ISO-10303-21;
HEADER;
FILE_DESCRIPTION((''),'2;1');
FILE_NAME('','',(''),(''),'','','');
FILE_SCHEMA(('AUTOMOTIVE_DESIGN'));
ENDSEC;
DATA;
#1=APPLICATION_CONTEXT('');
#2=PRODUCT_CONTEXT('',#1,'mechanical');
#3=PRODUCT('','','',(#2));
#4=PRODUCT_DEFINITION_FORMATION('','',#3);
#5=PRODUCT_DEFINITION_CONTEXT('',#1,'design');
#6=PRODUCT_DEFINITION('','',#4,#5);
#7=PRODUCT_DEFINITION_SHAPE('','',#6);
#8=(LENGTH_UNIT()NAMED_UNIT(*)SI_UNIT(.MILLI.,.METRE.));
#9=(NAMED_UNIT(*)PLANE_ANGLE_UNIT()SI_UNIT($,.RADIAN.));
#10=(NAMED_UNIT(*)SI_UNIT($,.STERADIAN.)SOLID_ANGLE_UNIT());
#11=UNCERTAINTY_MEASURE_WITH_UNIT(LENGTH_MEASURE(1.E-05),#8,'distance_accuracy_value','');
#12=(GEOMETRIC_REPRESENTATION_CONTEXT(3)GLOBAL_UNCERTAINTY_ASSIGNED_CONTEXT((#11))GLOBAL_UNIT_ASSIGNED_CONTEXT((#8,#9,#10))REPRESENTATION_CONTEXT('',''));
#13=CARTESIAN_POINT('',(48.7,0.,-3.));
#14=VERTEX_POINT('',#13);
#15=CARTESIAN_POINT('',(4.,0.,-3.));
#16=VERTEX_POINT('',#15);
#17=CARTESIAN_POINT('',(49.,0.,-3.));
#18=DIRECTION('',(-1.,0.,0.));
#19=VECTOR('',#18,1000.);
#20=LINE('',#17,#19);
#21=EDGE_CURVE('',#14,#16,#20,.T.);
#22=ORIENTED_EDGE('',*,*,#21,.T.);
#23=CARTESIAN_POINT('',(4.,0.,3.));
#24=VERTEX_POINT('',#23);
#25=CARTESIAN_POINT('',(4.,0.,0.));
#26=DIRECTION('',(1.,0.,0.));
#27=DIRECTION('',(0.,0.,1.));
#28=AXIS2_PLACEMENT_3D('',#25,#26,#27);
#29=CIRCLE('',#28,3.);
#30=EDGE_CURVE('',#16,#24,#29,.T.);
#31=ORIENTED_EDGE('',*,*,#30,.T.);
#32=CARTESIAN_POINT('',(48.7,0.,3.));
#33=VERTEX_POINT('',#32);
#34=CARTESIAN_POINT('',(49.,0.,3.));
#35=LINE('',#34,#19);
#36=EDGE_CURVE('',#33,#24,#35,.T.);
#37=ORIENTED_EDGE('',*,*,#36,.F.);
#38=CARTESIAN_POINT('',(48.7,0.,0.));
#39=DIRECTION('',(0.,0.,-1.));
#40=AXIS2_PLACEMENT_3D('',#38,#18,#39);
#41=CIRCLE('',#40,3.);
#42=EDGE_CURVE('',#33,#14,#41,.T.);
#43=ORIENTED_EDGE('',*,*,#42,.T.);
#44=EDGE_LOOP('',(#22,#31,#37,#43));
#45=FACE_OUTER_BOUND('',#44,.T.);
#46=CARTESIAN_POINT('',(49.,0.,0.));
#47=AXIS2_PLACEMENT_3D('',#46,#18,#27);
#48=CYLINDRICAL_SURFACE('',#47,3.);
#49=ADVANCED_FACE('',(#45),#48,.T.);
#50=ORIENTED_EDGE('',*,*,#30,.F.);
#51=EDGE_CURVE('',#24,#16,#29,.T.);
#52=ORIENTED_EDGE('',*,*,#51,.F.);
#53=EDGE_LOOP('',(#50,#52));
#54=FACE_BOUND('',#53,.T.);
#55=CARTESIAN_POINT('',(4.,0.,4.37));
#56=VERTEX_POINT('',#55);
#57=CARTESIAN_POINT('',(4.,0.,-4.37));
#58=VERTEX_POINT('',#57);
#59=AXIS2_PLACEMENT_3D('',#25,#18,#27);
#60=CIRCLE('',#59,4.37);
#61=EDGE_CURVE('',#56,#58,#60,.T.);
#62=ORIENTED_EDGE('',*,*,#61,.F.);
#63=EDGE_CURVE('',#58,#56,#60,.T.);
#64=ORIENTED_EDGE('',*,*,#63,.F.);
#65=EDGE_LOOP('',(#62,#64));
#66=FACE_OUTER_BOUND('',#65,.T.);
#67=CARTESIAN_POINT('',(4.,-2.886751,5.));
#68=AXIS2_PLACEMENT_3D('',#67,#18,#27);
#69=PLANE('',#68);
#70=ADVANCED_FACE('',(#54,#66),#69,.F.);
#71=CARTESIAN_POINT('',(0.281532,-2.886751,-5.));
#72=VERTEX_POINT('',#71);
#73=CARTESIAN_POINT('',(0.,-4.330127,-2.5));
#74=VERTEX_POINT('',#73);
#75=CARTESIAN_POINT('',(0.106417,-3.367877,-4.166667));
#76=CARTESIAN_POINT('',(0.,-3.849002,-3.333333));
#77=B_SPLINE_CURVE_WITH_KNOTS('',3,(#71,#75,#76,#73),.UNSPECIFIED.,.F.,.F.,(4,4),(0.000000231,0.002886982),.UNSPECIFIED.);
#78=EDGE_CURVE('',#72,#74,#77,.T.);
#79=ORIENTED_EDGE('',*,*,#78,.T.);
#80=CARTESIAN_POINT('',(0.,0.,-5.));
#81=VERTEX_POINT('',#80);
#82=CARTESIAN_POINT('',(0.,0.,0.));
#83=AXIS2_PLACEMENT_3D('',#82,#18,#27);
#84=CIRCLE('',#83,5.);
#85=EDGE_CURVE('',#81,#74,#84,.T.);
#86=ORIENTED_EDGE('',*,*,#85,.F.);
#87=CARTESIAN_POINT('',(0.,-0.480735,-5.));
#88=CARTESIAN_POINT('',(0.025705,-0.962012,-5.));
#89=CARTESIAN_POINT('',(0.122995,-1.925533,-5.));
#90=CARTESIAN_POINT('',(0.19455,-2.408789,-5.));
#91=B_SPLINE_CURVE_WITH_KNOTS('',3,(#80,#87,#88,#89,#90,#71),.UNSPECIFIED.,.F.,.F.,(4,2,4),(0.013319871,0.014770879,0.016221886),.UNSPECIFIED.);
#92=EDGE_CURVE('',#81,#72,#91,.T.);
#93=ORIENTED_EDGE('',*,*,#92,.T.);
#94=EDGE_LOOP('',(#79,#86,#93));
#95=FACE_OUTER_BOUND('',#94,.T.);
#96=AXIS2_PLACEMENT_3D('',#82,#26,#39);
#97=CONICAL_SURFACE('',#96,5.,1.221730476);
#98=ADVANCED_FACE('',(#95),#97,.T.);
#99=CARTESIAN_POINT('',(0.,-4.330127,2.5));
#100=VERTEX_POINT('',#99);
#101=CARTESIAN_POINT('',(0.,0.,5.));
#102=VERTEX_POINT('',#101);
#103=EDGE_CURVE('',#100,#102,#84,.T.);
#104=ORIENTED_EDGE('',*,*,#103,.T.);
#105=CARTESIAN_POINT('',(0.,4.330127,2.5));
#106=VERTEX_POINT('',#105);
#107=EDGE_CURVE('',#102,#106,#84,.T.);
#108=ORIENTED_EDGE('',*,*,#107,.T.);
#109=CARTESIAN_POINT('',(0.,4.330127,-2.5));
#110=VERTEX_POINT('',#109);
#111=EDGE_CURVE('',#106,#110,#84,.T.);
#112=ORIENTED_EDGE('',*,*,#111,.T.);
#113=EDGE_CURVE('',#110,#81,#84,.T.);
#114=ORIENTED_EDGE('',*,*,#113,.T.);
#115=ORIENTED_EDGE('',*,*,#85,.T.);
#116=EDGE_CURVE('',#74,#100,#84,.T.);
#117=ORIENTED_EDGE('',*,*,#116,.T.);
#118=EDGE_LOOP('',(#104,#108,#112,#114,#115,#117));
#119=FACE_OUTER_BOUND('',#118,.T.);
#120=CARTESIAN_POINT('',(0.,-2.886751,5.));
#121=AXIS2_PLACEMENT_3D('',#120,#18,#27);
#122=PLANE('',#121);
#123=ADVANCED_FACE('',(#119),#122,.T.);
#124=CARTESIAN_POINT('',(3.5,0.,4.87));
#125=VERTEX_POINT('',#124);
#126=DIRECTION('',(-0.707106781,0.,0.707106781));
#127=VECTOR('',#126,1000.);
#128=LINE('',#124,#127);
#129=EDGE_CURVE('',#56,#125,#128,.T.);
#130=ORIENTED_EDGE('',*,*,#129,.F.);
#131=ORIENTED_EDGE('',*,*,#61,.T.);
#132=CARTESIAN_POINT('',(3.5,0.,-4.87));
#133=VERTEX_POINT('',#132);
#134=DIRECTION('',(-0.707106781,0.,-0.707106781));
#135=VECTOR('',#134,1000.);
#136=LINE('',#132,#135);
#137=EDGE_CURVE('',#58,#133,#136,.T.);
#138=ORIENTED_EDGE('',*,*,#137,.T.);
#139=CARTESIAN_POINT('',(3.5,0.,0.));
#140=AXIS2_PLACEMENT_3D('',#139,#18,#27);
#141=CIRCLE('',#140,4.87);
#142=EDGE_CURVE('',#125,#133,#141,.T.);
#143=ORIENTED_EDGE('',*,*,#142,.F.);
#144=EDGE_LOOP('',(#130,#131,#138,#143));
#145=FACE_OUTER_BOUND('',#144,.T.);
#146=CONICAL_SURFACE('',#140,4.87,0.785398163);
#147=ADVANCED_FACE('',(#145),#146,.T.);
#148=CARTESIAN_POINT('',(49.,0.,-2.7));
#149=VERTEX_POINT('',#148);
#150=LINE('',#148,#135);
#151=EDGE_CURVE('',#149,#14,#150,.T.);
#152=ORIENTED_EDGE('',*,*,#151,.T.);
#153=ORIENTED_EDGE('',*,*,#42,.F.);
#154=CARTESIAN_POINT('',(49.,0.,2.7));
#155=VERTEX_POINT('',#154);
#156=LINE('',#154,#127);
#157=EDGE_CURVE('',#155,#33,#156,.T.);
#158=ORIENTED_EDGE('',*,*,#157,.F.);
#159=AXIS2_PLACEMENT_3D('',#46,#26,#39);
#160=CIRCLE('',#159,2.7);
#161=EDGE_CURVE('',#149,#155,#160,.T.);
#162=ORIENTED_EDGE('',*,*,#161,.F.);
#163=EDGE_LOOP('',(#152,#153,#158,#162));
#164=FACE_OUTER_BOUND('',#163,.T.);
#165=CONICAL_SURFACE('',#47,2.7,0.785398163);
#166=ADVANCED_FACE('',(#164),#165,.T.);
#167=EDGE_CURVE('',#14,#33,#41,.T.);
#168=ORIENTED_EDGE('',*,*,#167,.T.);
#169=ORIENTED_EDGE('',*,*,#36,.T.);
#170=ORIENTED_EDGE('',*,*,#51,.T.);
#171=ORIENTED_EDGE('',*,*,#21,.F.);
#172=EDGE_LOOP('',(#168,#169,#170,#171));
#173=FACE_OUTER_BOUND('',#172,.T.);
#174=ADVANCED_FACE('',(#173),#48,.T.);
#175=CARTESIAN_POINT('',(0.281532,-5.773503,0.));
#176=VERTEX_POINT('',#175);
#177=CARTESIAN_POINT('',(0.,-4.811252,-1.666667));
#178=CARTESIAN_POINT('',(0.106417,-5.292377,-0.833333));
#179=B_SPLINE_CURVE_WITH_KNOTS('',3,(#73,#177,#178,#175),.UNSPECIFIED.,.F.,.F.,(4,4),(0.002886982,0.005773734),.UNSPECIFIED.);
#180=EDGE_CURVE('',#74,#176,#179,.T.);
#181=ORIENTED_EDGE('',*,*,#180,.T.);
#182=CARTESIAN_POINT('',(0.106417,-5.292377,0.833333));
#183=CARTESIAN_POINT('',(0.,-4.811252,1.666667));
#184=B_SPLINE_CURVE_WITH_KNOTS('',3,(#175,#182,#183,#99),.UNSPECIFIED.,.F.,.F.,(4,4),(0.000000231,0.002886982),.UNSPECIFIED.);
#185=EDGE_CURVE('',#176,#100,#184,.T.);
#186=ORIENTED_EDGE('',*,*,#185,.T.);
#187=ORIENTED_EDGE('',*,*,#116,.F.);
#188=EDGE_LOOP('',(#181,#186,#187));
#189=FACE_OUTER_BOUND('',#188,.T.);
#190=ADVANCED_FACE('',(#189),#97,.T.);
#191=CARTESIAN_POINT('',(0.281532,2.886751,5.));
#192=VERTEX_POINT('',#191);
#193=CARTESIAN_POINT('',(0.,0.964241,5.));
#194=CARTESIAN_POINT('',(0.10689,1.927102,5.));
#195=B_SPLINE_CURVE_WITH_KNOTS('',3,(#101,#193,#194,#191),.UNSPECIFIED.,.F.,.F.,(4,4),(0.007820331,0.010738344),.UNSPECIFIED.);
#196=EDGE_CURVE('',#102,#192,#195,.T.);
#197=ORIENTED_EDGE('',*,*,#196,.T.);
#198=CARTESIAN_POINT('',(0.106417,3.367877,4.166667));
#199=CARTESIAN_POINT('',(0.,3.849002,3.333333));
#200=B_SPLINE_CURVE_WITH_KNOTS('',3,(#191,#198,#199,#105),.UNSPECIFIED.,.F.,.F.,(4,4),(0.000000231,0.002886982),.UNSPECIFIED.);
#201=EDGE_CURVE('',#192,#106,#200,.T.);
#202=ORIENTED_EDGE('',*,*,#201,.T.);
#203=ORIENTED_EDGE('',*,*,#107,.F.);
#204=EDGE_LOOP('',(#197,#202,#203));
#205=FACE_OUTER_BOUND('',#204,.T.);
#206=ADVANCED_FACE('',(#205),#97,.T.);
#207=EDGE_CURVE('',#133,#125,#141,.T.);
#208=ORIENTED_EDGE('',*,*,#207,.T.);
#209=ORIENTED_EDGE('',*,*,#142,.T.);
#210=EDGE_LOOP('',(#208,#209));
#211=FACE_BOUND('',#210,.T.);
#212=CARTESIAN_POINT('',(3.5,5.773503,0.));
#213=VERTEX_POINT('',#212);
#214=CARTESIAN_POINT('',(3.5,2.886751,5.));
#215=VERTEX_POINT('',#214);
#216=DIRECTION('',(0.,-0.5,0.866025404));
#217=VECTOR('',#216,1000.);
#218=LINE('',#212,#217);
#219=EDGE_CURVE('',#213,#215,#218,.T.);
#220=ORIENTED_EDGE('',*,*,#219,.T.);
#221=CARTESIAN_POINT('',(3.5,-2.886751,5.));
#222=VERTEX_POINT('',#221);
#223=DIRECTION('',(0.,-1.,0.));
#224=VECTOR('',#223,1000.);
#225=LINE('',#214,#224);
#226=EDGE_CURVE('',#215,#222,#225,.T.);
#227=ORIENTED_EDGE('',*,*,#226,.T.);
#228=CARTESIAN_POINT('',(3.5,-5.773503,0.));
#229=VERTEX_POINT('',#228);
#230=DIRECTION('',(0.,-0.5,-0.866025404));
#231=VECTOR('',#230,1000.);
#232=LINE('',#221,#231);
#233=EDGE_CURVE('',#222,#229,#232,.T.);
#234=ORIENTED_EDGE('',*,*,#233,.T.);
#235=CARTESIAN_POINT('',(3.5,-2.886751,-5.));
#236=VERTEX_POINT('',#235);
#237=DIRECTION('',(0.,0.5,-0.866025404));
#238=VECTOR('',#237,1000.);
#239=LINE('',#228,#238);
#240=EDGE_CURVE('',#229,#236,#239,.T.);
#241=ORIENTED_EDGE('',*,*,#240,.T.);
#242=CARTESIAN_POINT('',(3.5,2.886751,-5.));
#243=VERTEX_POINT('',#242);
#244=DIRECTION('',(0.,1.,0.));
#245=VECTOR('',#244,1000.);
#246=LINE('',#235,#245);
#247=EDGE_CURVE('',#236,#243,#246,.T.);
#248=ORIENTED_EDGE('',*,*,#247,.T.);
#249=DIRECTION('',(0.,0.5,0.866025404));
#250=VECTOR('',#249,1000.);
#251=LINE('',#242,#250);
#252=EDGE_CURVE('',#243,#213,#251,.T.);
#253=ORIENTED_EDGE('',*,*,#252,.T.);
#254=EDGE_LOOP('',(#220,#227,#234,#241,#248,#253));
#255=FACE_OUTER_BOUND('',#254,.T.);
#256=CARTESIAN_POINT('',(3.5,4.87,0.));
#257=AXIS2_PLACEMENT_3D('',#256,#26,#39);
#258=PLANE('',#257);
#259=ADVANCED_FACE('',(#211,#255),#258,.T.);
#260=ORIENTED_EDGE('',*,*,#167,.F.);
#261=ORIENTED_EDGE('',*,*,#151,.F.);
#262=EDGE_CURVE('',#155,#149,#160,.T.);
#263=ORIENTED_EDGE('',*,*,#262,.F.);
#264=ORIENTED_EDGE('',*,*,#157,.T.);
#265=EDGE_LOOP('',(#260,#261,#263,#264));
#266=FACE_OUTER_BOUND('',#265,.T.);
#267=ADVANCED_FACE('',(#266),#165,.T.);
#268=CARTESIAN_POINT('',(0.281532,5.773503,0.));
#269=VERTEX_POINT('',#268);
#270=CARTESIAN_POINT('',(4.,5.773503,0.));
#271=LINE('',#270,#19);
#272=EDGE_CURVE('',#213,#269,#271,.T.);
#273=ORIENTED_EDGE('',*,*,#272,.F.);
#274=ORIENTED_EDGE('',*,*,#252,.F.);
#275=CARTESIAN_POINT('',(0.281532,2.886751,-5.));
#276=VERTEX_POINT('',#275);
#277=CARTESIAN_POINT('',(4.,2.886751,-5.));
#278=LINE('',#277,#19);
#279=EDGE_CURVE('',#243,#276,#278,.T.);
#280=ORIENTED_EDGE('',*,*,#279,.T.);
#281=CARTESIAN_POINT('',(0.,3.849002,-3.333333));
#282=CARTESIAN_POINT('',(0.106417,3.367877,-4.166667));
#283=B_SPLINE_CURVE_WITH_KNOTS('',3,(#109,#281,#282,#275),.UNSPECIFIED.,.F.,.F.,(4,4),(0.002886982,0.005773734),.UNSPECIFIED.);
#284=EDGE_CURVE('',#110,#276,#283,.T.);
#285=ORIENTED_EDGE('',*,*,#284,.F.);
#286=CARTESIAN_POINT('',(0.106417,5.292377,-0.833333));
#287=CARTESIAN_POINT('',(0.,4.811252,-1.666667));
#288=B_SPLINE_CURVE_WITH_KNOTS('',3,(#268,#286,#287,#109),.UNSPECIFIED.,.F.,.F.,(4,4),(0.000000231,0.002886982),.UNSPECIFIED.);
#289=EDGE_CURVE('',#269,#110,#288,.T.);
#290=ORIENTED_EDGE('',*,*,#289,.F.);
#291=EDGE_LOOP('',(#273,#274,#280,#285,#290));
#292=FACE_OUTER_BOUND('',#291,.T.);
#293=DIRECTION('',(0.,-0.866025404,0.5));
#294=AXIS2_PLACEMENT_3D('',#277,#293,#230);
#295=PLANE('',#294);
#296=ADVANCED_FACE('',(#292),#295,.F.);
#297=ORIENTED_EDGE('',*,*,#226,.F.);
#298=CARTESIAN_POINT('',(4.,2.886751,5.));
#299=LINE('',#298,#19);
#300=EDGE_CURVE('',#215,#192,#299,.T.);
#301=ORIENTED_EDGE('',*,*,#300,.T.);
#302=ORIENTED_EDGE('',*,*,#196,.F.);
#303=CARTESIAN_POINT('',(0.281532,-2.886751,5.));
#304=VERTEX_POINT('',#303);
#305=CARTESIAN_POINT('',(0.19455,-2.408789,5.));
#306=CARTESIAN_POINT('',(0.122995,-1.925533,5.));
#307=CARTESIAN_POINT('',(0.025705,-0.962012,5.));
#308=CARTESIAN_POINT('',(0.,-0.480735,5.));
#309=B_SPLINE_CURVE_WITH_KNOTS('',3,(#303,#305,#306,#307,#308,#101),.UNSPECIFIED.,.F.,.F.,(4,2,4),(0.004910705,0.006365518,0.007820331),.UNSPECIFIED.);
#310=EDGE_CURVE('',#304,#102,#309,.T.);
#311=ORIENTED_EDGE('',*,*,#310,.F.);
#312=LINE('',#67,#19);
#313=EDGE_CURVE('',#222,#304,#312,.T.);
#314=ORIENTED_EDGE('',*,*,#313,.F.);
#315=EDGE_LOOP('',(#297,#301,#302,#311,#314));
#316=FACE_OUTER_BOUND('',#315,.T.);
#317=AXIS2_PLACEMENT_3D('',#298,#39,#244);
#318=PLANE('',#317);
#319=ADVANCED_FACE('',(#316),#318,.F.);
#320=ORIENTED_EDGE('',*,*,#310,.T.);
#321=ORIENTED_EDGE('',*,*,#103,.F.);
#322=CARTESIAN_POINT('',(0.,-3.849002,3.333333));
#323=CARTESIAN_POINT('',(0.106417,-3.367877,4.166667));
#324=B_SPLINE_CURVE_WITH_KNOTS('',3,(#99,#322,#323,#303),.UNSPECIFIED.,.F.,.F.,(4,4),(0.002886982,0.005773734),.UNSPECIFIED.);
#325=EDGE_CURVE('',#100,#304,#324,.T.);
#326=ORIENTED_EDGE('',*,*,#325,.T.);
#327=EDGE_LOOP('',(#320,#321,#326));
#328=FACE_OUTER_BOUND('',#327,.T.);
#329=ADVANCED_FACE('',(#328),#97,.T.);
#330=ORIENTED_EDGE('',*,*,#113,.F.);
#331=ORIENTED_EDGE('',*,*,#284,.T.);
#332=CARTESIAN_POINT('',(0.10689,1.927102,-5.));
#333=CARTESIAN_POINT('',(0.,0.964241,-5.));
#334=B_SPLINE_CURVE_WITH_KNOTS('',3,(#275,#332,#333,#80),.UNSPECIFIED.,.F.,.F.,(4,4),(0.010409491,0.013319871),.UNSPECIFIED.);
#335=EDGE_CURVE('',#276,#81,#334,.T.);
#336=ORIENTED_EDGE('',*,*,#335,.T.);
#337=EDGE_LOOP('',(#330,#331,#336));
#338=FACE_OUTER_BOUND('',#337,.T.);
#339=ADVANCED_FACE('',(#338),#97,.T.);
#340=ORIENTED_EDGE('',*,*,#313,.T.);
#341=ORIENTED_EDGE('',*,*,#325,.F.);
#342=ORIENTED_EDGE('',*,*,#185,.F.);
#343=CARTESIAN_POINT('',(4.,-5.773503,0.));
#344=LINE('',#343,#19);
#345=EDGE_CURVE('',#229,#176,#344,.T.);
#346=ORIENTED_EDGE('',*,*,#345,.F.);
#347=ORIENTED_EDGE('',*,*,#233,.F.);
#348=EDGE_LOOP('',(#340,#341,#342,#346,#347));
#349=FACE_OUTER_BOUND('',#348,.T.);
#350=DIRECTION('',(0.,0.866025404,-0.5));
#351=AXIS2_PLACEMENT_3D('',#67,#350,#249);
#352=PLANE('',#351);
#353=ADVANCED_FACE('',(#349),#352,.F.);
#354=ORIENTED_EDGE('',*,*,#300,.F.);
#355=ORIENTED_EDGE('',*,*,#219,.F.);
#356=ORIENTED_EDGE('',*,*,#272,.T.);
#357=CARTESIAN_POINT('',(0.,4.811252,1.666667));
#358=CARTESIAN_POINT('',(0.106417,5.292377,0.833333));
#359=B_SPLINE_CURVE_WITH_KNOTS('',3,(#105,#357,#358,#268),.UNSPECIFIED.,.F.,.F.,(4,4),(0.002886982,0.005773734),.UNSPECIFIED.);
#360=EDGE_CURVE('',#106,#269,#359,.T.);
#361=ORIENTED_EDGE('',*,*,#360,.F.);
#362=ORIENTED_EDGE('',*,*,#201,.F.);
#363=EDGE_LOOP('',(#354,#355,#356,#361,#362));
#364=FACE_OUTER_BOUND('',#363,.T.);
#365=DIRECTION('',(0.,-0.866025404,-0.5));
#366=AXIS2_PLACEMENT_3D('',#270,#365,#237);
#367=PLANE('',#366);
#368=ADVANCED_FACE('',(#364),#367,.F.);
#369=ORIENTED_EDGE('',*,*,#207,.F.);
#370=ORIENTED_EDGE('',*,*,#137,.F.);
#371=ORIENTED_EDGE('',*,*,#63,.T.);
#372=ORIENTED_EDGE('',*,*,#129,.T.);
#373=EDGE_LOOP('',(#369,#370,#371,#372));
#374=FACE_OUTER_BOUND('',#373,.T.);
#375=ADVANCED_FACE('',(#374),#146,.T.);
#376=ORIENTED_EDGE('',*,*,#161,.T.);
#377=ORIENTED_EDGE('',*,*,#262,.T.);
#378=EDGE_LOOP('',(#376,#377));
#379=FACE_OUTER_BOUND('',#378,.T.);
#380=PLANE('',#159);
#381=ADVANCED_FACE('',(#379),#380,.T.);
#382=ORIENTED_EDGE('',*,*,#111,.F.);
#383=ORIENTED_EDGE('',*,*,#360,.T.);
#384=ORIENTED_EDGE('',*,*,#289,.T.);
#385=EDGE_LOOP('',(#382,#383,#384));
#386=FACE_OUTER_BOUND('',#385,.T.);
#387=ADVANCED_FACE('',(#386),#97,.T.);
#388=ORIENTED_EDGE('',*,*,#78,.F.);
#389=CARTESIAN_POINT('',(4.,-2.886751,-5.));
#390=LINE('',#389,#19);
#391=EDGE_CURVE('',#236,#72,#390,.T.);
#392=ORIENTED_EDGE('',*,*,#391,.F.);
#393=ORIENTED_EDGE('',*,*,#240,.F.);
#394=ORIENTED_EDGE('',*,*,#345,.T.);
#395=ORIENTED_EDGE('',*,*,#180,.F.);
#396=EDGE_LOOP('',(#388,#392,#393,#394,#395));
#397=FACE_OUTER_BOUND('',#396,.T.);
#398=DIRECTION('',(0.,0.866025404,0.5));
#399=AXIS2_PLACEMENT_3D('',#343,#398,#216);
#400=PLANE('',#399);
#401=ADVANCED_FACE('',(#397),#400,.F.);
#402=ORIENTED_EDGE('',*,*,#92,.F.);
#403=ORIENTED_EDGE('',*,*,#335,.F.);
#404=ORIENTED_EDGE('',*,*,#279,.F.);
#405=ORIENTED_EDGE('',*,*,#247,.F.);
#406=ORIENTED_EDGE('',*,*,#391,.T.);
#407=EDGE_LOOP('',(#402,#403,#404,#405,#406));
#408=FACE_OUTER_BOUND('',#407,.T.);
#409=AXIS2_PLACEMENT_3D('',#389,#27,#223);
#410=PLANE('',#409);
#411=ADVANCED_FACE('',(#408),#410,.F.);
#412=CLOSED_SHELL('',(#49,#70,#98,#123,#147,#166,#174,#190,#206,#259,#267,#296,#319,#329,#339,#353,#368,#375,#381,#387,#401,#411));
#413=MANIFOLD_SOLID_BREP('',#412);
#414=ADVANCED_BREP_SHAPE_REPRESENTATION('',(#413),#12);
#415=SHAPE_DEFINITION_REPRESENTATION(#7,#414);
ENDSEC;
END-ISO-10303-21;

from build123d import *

# Parameters (mm, degrees)
BASEHEAD_DEPTH = 4
SKETCH5_R      = 3
BASEBODY_DEPTH = 45
CHAMFER1_SIZE  = 0.3


with BuildPart() as part:
    # Sketch2 → BaseHead (new body)
    with BuildSketch(Plane(origin=(0, 0, 0), x_dir=(0, 0, -1), z_dir=(1, 0, 0))):
        Polygon((0, -5.773502692), (5, -2.886751346), (5, 2.886751346), (0, 5.773502692), (-5, 2.886751346), (-5, -2.886751346), align=None)
    extrude(amount=BASEHEAD_DEPTH)

    # Sketch3 → BearingFace (revolve, cut)
    with BuildSketch(Plane.XY, mode=Mode.PRIVATE) as bearingface_sk:
        Polygon((4, 5.773502692), (4, 4.37), (3.5, 4.87), (3.5, 5.773502692), align=None)
    revolve(bearingface_sk.sketch.rotate(Axis((-0.957090588, 0, 0), (1, 0, 0)), 90), axis=Axis((-0.957090588, 0, 0), (1, 0, 0)), mode=Mode.SUBTRACT)

    # Sketch4 → HeadChamfer (revolve, cut)
    with BuildSketch(Plane.XY):
        Polygon((0, 5.773502692), (0.281531956, 5.773502692), (0, 5), align=None)
    revolve(axis=Axis((-0.493528746, 0, 0), (1, 0, 0)), mode=Mode.SUBTRACT)

    # Sketch5 → BaseBody (add)
    with BuildSketch(Plane(origin=(4, 0, 0), x_dir=(0, 0, -1), z_dir=(1, 0, 0))):
        with Locations(Location((0, 0, 0), (0, 0, 180))):
            Circle(SKETCH5_R)
    extrude(amount=BASEBODY_DEPTH)

    # Chamfer1
    chamfer1_edges = [part.edges().sort_by_distance(p)[0] for p in [
        (49, 0, -3),
    ]]
    chamfer(chamfer1_edges, length=CHAMFER1_SIZE)


solid = part.part
